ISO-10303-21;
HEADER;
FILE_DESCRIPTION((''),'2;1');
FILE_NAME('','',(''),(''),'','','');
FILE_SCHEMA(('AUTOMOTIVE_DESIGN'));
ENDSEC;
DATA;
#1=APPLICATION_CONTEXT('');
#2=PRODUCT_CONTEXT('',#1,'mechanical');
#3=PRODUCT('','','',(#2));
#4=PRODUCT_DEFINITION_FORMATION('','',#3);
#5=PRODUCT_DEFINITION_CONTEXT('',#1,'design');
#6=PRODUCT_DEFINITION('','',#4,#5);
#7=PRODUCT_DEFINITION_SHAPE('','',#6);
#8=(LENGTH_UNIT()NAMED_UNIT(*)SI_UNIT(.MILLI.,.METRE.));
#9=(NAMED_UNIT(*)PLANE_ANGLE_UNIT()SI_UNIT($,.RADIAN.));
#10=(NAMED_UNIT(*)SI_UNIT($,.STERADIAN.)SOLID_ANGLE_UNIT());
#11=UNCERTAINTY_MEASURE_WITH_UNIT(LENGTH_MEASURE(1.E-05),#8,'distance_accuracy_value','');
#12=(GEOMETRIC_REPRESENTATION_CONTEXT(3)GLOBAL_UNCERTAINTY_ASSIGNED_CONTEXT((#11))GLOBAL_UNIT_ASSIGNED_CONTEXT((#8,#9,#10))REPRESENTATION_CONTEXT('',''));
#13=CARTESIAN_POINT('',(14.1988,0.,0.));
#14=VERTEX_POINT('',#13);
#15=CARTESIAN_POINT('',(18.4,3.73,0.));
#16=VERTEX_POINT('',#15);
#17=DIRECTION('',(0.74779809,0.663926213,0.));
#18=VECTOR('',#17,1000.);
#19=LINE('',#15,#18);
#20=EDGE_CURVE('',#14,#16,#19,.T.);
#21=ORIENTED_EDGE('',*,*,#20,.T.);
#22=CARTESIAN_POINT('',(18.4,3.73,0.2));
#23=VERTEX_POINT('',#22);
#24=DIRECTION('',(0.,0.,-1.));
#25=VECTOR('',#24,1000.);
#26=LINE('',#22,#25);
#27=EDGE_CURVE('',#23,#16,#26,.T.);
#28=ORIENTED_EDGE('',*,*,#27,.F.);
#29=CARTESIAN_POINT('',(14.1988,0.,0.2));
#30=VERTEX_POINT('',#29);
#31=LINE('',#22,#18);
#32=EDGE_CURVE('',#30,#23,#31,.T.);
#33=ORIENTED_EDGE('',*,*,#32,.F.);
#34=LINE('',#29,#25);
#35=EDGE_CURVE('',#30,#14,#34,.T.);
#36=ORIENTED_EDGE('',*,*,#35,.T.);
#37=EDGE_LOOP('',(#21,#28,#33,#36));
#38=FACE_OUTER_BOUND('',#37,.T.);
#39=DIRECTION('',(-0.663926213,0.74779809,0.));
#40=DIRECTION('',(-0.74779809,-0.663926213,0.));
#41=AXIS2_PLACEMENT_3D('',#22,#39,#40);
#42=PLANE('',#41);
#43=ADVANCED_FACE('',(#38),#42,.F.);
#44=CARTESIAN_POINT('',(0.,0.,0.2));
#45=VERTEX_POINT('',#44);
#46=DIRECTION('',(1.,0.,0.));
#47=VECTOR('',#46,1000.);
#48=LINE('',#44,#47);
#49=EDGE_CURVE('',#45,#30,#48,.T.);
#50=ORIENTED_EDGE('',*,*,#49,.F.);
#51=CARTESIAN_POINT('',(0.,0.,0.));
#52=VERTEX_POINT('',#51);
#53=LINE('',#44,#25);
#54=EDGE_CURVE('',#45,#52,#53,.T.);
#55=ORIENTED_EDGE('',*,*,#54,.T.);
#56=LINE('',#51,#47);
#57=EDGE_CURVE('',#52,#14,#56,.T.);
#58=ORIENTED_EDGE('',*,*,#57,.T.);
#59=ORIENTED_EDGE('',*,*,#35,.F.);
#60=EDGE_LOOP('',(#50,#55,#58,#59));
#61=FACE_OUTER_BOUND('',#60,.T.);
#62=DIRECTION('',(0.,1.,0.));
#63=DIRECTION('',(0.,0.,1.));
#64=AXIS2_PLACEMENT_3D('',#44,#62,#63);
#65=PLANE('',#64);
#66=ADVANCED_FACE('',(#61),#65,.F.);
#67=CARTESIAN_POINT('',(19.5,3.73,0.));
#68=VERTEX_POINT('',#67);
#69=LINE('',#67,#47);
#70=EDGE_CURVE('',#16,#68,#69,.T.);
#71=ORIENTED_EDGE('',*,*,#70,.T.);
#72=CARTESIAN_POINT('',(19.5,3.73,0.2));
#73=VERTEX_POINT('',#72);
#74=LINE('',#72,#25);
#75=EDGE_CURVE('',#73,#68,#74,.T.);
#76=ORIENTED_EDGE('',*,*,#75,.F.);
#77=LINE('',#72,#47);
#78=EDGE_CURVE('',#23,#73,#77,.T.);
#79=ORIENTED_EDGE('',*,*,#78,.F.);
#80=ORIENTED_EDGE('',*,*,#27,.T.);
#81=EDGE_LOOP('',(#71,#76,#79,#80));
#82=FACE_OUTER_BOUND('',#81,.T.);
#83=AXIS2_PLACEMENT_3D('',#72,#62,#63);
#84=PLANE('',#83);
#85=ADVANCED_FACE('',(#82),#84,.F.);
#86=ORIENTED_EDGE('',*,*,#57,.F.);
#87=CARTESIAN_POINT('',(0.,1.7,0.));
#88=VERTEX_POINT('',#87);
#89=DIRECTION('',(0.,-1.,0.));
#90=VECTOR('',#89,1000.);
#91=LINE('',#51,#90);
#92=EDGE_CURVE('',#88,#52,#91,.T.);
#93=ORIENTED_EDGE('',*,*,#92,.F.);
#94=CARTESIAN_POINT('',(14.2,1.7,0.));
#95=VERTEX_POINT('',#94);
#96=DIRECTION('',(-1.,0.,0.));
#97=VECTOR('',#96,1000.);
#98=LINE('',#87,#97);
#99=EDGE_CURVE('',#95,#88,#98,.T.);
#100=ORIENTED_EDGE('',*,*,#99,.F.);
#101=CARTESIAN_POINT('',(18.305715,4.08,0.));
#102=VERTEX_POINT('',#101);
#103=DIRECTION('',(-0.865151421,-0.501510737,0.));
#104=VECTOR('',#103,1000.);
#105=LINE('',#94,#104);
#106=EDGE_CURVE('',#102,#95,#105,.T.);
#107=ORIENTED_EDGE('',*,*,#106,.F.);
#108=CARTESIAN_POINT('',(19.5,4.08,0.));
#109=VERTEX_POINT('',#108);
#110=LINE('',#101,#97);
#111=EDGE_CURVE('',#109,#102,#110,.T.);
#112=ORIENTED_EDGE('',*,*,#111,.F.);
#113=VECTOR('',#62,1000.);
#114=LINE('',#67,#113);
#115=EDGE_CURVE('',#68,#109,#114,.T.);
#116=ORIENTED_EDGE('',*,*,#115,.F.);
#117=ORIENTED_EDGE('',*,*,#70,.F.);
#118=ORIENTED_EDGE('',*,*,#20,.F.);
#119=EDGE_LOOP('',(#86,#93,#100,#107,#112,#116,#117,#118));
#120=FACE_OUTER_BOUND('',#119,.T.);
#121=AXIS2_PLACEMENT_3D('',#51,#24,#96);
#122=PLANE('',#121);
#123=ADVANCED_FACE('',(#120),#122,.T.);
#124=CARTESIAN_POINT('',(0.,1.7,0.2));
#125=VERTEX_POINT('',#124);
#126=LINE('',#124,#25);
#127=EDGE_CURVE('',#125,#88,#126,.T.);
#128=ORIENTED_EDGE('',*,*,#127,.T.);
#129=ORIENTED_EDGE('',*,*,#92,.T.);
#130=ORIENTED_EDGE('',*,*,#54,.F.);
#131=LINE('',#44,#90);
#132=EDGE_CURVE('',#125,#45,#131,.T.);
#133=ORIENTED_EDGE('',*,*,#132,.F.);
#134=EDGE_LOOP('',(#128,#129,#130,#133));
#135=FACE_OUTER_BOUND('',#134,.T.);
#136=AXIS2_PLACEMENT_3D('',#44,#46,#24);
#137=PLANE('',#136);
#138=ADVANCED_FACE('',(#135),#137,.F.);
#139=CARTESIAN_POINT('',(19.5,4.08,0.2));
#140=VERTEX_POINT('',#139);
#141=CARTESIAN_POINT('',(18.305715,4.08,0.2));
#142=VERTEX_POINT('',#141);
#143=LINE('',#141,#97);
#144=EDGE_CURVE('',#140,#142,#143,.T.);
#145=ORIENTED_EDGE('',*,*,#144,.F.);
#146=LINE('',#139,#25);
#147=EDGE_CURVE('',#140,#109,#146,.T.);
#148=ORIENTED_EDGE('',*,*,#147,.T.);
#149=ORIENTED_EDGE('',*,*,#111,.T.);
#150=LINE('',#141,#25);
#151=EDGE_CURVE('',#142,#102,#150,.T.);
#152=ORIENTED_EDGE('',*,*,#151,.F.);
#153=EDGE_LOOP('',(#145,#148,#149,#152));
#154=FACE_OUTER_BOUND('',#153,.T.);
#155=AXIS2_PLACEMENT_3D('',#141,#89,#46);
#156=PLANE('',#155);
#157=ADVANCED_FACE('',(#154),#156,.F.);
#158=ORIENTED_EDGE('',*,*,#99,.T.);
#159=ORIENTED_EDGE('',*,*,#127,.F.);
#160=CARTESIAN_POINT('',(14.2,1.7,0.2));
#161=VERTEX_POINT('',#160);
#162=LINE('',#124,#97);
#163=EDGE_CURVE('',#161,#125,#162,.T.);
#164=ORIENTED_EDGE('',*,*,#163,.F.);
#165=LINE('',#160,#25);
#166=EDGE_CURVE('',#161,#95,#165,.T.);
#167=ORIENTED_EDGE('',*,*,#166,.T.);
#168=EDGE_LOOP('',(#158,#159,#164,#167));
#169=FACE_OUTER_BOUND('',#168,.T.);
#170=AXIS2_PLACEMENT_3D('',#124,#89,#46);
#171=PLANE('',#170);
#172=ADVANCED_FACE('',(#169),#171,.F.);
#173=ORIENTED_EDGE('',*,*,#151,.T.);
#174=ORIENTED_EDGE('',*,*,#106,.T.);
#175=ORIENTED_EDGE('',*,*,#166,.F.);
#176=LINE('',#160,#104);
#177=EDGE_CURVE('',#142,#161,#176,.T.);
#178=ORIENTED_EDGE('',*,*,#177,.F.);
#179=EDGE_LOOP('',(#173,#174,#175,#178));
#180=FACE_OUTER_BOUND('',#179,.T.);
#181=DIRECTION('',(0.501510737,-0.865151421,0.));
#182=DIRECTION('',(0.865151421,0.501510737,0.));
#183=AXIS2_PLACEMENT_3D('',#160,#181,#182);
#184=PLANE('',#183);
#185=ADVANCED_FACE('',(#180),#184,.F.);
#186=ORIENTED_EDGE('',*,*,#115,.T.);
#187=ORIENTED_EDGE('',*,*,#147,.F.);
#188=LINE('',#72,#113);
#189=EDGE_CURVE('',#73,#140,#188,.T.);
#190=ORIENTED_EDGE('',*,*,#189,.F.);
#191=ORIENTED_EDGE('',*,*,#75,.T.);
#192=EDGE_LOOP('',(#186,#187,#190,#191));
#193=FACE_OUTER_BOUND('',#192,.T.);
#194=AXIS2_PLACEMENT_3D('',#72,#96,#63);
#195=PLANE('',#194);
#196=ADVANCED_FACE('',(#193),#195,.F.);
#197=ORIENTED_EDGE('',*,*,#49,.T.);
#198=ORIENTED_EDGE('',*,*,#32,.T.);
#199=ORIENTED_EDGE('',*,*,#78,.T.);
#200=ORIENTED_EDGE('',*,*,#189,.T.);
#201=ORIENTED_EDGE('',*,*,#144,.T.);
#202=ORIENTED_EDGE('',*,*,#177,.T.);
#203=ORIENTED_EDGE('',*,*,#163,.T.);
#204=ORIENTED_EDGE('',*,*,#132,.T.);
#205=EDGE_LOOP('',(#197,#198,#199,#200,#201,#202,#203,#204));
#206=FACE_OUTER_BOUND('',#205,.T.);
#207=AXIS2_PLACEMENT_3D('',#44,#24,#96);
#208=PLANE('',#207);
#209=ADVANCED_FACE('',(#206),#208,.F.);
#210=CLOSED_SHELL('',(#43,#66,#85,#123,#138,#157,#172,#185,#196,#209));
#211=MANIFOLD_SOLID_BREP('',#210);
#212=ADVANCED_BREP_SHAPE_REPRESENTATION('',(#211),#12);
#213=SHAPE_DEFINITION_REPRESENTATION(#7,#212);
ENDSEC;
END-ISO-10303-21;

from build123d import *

# Parameters (mm, degrees)
BOSS_EXTRUDE1_DEPTH = 0.2


with BuildPart() as part:
    # Sketch1 → Boss-Extrude1 (new body)
    with BuildSketch(Plane.XY):
        Polygon((14.2, 1.7), (18.305715448, 4.08), (19.5, 4.08), (19.5, 3.73), (18.4, 3.73), (14.19879989, 0), (0, 0), (0, 1.7), align=None)
    extrude(amount=BOSS_EXTRUDE1_DEPTH)


solid = part.part
